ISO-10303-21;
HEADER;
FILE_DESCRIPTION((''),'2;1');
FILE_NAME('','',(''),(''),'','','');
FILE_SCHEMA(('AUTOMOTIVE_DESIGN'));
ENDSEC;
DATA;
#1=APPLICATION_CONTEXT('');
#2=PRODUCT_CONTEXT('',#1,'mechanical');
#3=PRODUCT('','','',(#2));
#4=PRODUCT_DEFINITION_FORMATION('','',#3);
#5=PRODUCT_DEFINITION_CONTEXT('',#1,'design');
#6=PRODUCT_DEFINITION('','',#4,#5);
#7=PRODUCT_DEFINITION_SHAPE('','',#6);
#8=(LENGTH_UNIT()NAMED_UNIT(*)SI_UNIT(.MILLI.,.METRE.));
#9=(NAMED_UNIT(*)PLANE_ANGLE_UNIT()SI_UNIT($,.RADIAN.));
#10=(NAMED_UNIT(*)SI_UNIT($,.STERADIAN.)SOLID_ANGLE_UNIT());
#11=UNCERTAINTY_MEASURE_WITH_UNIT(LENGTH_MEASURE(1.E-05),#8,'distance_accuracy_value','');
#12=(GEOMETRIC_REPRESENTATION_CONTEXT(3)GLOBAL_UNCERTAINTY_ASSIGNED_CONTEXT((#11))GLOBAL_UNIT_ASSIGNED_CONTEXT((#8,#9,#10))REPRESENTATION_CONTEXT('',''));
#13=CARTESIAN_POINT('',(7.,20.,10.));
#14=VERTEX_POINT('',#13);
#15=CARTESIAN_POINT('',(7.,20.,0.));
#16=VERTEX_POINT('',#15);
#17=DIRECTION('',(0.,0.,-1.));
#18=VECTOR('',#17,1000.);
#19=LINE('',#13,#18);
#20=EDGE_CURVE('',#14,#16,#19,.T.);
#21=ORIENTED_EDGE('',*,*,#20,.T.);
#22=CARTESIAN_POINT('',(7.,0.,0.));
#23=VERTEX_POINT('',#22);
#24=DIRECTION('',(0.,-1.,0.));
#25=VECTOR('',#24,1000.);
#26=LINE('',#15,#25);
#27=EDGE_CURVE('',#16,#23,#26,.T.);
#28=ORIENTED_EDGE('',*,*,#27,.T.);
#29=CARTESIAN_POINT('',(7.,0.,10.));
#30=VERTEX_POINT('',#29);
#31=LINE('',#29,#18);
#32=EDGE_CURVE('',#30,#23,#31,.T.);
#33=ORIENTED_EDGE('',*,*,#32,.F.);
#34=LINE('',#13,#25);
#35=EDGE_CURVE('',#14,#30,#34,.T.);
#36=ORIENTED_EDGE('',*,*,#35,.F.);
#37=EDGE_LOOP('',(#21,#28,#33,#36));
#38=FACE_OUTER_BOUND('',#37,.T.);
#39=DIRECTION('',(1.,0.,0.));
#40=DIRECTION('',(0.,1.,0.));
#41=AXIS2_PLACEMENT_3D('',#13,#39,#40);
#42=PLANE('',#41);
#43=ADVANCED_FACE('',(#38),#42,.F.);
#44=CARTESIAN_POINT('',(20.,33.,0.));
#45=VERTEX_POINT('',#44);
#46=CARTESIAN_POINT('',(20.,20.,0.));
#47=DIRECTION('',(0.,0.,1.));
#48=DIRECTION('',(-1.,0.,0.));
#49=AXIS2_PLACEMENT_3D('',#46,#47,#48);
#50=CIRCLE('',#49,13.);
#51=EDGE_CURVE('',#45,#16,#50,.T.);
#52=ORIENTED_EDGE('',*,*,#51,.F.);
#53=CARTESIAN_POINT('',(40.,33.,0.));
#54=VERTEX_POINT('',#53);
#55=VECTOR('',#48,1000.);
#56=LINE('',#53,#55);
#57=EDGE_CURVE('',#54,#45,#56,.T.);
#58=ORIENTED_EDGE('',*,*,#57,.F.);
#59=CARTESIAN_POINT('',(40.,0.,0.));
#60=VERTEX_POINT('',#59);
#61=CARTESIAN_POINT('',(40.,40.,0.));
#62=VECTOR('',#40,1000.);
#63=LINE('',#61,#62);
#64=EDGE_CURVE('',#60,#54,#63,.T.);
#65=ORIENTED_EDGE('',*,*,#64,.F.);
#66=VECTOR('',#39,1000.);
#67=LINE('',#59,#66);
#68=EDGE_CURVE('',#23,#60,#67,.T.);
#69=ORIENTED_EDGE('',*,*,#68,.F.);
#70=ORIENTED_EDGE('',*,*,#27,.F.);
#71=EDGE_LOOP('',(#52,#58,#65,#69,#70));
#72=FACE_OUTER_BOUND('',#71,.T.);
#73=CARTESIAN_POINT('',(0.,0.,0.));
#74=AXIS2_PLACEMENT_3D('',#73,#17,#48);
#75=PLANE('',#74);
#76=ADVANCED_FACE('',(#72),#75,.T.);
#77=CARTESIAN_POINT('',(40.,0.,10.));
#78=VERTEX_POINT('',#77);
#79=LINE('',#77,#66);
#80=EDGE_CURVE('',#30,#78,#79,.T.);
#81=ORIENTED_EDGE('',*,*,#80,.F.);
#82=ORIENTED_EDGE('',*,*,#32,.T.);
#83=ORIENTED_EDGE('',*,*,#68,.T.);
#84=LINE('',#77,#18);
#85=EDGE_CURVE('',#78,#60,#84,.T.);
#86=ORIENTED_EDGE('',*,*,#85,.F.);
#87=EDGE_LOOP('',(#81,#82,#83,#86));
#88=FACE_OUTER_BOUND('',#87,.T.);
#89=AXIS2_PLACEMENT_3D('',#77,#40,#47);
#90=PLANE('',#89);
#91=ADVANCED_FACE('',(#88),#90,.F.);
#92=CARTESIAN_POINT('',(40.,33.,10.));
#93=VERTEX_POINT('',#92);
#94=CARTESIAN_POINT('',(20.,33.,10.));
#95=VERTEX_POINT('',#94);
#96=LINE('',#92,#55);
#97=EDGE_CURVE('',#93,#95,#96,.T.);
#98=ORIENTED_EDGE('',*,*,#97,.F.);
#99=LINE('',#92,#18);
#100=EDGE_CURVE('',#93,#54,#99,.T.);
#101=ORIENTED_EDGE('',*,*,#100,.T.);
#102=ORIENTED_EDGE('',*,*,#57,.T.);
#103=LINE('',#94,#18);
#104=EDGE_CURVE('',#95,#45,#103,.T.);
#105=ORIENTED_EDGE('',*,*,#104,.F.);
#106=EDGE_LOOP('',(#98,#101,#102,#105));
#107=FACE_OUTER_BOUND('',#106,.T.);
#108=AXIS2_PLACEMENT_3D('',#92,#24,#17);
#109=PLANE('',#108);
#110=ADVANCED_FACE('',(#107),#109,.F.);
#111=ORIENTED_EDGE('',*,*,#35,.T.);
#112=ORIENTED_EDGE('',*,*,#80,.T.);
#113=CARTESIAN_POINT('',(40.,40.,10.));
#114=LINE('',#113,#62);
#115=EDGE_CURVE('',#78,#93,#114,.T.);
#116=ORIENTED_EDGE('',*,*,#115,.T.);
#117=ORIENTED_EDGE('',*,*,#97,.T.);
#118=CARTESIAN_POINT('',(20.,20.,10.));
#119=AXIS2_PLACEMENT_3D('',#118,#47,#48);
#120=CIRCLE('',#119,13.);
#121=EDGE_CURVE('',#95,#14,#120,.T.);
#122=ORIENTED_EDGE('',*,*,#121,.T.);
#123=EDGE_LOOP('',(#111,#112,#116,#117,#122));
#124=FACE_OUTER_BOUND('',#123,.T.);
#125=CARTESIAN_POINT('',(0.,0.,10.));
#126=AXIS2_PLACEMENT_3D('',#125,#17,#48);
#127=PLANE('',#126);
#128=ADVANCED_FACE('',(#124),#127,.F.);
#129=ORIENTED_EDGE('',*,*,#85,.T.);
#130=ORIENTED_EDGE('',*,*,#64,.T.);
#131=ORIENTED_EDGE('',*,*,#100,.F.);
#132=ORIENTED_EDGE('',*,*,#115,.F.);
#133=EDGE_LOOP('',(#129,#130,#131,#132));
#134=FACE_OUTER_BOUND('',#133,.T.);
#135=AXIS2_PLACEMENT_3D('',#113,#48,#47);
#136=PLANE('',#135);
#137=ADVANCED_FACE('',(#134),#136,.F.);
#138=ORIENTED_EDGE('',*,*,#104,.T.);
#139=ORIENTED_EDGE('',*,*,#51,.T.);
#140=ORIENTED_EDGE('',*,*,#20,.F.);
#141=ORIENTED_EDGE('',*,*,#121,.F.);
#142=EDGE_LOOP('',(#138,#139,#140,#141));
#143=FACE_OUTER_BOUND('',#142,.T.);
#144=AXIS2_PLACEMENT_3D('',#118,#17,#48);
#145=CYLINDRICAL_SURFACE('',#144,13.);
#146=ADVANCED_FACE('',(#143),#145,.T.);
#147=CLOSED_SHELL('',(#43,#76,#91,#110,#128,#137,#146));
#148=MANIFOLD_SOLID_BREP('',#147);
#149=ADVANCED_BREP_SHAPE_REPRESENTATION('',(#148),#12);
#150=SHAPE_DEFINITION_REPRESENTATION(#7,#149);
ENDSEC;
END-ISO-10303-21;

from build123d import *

# Parameters (mm, degrees)
SKETCH1_W           = 40
SKETCH1_H           = 40
BOSS_EXTRUDE1_DEPTH = 10
FILLET1_R           = 20
CUT_EXTRUDE1_DEPTH  = 58.445626465


with BuildPart() as part:
    # Sketch1 → Boss-Extrude1 (new body)
    with BuildSketch(Plane.XY):
        with Locations((20, 20)):
            Rectangle(SKETCH1_W, SKETCH1_H)
    extrude(amount=BOSS_EXTRUDE1_DEPTH)

    # Fillet1
    fillet1_edges = [part.edges().sort_by_distance(p)[0] for p in [
        (0, 40, 5),
    ]]
    fillet(fillet1_edges, radius=FILLET1_R)

    # Sketch2 → Cut-Extrude1 (cut, through all)
    with BuildSketch(Plane(origin=(0, 0, 0), x_dir=(-1, 0, 0), z_dir=(0, 0, -1))):
        with BuildLine():
            Line((-40, 40), (-20, 40))
            ThreePointArc((-20, 40), (-5.857864376, 34.142135624), (0, 20))
            Line((0, 20), (0, 0))
            Line((0, 0), (-7, 0))
            Line((-7, 0), (-7, 20))
            ThreePointArc((-7, 20), (-10.807611845, 29.192388155), (-20, 33))
            Line((-20, 33), (-40, 33))
            Line((-40, 33), (-40, 40))
        make_face()
    extrude(amount=-CUT_EXTRUDE1_DEPTH, mode=Mode.SUBTRACT)


solid = part.part
